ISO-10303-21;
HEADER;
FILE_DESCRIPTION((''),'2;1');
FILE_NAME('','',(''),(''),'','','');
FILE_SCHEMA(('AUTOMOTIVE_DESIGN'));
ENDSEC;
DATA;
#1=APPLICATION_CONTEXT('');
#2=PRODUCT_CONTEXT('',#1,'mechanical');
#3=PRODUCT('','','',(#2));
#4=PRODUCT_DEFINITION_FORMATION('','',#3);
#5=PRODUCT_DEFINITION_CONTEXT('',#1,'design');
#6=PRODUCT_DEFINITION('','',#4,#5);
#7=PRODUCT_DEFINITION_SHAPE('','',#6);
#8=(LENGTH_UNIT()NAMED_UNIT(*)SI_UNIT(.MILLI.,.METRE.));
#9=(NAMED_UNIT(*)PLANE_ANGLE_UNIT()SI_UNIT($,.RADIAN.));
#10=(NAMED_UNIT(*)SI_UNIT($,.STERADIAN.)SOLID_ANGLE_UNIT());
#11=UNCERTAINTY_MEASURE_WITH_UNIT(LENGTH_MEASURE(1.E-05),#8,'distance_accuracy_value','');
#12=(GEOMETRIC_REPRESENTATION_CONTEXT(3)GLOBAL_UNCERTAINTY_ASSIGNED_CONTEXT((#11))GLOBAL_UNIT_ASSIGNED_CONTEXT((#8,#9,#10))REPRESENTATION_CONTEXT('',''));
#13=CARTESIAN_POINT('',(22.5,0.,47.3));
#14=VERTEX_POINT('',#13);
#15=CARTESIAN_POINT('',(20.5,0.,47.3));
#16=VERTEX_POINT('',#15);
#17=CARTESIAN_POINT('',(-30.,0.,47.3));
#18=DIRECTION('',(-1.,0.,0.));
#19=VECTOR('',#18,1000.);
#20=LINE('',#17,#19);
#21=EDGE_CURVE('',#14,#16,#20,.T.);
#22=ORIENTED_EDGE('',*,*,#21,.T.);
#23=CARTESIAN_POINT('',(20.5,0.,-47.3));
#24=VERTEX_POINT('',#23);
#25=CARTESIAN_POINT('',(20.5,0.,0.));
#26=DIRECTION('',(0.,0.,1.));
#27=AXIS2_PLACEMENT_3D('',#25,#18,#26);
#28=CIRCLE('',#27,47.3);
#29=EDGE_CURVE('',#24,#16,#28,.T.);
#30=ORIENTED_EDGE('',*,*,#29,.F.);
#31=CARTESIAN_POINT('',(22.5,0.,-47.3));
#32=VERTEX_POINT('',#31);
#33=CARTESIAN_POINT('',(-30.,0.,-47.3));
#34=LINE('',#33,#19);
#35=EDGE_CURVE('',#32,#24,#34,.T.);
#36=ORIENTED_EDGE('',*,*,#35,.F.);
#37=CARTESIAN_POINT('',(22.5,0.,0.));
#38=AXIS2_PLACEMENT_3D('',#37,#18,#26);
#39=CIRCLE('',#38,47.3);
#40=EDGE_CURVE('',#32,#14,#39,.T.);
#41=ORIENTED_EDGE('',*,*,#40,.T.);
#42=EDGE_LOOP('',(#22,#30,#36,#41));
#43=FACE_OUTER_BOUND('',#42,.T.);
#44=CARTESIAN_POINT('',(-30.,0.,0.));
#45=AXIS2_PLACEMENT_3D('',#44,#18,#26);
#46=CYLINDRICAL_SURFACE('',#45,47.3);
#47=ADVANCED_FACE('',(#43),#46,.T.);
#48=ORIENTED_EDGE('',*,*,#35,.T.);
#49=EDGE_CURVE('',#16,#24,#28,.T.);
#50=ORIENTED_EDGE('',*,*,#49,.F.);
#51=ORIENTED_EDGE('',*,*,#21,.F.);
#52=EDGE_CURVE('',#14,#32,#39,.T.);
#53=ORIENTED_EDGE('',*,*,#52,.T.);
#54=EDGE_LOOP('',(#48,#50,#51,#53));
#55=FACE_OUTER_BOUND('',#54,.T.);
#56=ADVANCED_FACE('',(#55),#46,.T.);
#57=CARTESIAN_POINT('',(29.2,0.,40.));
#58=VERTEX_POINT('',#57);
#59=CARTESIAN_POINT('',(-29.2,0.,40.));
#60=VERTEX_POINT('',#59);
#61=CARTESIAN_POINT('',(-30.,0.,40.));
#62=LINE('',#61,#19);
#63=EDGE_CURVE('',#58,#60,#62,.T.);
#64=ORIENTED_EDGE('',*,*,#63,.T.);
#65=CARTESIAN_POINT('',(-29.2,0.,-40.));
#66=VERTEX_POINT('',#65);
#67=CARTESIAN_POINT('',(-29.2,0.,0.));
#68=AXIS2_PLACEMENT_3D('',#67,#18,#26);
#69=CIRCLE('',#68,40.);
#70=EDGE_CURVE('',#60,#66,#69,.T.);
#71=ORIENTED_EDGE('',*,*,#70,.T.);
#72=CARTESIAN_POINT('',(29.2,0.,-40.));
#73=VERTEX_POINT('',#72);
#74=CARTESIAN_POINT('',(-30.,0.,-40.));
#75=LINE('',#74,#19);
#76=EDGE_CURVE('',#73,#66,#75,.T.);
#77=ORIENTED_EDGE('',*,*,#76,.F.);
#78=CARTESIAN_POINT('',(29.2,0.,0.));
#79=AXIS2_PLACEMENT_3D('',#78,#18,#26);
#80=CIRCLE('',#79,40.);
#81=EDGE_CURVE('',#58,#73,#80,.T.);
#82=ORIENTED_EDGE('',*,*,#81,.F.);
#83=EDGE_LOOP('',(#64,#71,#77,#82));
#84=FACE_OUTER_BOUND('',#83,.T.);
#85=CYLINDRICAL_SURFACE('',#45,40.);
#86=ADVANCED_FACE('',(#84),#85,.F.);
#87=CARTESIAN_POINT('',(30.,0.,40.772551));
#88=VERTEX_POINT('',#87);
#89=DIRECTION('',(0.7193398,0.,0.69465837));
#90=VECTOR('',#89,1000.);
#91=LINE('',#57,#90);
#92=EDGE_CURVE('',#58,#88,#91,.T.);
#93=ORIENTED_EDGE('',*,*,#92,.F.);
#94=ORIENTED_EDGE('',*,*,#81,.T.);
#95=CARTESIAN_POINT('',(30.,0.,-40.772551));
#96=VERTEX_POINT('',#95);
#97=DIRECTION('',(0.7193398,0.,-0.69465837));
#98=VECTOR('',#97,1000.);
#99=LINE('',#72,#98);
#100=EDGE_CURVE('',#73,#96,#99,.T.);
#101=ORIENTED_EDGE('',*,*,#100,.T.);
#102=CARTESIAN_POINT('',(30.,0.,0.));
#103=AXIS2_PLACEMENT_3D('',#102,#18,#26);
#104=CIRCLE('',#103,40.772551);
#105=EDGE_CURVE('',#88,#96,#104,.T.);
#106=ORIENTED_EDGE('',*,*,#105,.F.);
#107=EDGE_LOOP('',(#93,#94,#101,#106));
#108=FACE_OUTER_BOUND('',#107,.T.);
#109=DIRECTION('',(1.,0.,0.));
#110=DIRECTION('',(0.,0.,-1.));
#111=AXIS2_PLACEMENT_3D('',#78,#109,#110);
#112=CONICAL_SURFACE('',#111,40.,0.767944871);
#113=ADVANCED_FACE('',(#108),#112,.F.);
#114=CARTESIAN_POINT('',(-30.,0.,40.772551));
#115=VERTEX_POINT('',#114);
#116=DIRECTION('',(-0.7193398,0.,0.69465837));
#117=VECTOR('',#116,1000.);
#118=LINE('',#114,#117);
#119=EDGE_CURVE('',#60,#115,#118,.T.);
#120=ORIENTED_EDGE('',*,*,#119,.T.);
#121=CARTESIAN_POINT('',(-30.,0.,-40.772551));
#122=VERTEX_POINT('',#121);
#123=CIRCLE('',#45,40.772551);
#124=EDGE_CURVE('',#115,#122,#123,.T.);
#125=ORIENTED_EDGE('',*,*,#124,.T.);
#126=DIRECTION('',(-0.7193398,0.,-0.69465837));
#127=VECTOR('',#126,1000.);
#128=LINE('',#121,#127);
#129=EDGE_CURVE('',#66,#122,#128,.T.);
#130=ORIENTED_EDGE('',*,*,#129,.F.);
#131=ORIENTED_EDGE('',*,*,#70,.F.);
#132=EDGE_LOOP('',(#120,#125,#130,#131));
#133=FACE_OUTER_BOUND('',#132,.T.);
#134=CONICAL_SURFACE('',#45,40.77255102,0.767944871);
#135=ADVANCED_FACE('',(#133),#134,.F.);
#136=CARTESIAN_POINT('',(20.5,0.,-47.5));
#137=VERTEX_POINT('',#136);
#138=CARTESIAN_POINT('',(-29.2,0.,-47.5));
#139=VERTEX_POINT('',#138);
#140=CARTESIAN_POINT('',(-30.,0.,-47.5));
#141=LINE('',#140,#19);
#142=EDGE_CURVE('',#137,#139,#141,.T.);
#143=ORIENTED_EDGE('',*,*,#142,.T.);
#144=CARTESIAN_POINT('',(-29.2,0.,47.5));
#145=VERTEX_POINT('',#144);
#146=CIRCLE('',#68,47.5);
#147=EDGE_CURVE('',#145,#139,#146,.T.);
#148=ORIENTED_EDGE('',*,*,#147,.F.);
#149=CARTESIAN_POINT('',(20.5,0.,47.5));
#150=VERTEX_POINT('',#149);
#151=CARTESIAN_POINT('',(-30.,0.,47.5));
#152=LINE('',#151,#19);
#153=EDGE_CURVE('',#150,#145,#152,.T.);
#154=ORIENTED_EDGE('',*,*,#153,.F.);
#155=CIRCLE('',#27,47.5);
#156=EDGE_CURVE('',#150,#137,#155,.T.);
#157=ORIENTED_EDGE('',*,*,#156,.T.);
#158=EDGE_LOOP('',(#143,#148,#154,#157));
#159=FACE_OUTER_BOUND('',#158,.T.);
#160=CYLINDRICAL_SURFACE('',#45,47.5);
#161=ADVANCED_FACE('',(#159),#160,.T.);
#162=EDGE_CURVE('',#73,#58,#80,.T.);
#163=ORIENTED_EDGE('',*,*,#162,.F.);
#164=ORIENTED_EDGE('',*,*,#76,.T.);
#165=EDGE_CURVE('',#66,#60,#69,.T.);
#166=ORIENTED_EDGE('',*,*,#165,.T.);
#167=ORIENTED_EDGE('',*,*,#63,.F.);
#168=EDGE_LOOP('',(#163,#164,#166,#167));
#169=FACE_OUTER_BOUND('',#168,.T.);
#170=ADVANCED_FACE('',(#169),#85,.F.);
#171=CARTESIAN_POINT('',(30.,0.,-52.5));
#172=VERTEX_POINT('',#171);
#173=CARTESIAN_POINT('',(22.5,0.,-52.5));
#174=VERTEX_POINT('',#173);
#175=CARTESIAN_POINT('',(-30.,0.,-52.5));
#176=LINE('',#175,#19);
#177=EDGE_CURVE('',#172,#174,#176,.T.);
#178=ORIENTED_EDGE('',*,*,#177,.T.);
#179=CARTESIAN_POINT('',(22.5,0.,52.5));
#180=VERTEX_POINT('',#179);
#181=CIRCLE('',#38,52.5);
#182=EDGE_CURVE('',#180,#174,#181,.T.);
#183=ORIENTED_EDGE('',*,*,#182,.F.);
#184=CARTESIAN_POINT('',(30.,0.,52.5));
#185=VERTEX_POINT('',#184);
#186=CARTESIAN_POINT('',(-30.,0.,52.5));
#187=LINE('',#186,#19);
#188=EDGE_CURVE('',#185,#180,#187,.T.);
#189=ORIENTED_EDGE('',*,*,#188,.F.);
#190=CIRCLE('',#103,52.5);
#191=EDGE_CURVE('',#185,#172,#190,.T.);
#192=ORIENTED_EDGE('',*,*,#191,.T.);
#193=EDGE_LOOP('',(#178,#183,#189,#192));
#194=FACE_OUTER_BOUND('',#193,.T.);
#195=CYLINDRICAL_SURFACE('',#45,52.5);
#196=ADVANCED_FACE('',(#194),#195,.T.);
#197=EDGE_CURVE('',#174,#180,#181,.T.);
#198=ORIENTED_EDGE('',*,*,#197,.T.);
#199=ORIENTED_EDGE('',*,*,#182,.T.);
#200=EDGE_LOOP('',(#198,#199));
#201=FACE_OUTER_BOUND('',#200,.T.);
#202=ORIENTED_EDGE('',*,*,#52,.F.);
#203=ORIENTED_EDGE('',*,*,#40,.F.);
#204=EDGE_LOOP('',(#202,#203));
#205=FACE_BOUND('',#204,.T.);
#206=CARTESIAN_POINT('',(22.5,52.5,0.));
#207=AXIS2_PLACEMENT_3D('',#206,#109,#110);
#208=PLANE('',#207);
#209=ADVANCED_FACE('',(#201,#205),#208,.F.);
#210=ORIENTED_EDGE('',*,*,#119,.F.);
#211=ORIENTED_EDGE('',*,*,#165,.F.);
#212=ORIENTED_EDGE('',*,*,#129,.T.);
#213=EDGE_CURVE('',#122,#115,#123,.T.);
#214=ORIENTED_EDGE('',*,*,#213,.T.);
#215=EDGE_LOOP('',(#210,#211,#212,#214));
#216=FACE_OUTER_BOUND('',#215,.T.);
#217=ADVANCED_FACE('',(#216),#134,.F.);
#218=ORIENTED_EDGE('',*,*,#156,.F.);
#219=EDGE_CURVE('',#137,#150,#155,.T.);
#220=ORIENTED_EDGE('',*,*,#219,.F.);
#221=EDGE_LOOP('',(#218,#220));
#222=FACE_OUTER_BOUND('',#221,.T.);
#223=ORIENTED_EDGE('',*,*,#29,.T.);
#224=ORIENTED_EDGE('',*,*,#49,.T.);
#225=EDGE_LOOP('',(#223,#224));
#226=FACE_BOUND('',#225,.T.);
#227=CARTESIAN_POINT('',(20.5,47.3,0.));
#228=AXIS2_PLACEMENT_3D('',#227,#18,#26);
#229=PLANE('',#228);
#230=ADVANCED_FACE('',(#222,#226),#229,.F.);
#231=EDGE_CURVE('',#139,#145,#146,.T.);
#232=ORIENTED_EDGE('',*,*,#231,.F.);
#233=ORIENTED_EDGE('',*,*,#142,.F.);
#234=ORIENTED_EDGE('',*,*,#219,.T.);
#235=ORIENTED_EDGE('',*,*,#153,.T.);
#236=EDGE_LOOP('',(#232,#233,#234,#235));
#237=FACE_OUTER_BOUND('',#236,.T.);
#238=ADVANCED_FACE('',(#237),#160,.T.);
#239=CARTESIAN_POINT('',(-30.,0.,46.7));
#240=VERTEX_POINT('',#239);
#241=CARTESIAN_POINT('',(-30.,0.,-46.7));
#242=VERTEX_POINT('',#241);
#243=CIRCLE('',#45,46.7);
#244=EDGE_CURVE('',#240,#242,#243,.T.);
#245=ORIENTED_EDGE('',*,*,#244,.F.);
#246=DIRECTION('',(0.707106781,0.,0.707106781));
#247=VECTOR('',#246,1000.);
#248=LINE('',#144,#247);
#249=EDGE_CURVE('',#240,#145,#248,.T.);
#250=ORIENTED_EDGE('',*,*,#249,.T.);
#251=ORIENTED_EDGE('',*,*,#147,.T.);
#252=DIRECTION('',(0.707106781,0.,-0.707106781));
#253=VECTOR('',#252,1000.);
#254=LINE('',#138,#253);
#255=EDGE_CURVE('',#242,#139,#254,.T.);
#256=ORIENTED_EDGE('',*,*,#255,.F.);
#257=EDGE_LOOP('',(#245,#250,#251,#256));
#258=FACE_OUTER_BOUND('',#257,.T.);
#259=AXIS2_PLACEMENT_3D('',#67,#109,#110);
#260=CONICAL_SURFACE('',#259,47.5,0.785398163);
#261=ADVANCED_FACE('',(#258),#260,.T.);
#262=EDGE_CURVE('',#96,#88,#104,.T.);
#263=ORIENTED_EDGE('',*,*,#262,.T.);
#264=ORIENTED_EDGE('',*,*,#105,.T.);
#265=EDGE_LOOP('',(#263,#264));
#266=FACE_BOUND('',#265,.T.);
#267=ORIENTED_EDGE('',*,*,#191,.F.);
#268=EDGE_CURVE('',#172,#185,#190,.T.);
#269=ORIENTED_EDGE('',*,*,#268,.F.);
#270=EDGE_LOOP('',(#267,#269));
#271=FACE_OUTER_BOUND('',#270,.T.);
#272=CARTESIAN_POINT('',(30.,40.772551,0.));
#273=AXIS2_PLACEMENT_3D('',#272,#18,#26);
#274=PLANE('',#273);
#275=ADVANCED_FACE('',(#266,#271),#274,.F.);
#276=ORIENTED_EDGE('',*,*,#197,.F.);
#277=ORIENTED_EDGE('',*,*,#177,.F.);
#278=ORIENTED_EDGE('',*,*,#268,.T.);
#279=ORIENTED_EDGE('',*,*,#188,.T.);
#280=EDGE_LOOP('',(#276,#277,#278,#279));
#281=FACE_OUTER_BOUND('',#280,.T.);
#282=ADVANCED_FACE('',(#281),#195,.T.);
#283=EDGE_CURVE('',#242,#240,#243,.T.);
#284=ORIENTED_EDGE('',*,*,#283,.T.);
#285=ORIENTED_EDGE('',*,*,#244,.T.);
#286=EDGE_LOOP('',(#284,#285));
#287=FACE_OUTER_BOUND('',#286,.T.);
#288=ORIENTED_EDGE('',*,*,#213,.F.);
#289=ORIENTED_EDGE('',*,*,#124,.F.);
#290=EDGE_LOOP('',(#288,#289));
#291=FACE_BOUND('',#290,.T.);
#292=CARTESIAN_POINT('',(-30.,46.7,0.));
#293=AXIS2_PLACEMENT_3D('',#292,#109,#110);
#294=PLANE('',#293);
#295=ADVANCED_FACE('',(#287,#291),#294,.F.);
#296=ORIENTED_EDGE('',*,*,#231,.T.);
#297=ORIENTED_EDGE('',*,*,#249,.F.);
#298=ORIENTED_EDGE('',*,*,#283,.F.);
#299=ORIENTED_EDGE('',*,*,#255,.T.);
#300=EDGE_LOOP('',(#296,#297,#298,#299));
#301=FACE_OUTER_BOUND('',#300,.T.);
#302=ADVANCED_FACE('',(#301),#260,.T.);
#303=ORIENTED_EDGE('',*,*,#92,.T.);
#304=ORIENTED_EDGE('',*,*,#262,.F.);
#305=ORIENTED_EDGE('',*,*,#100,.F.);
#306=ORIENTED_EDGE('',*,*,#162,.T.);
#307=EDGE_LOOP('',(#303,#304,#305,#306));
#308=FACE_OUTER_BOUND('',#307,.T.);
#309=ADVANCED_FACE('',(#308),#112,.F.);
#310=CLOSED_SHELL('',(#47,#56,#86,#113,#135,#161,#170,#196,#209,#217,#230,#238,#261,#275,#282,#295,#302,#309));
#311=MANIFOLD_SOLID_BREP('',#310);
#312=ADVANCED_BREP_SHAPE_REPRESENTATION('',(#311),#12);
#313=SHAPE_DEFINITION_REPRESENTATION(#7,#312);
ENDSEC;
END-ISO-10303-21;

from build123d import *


with BuildPart() as part:
    # Sketch 181 → 旋转1 (revolve)
    with BuildSketch(Plane.XY, mode=Mode.PRIVATE) as revolve_1_sk:
        Polygon((-30, 40.77255102), (-29.2, 40), (29.2, 40), (30, 40.77255102), (30, 52.5), (22.5, 52.5), (22.5, 47.3), (20.5, 47.3), (20.5, 47.5), (-29.2, 47.5), (-30, 46.7), align=None)
    revolve(revolve_1_sk.sketch.rotate(Axis((-30, 0, 0), (1, 0, 0)), 90), axis=Axis((-30, 0, 0), (1, 0, 0)))


solid = part.part
